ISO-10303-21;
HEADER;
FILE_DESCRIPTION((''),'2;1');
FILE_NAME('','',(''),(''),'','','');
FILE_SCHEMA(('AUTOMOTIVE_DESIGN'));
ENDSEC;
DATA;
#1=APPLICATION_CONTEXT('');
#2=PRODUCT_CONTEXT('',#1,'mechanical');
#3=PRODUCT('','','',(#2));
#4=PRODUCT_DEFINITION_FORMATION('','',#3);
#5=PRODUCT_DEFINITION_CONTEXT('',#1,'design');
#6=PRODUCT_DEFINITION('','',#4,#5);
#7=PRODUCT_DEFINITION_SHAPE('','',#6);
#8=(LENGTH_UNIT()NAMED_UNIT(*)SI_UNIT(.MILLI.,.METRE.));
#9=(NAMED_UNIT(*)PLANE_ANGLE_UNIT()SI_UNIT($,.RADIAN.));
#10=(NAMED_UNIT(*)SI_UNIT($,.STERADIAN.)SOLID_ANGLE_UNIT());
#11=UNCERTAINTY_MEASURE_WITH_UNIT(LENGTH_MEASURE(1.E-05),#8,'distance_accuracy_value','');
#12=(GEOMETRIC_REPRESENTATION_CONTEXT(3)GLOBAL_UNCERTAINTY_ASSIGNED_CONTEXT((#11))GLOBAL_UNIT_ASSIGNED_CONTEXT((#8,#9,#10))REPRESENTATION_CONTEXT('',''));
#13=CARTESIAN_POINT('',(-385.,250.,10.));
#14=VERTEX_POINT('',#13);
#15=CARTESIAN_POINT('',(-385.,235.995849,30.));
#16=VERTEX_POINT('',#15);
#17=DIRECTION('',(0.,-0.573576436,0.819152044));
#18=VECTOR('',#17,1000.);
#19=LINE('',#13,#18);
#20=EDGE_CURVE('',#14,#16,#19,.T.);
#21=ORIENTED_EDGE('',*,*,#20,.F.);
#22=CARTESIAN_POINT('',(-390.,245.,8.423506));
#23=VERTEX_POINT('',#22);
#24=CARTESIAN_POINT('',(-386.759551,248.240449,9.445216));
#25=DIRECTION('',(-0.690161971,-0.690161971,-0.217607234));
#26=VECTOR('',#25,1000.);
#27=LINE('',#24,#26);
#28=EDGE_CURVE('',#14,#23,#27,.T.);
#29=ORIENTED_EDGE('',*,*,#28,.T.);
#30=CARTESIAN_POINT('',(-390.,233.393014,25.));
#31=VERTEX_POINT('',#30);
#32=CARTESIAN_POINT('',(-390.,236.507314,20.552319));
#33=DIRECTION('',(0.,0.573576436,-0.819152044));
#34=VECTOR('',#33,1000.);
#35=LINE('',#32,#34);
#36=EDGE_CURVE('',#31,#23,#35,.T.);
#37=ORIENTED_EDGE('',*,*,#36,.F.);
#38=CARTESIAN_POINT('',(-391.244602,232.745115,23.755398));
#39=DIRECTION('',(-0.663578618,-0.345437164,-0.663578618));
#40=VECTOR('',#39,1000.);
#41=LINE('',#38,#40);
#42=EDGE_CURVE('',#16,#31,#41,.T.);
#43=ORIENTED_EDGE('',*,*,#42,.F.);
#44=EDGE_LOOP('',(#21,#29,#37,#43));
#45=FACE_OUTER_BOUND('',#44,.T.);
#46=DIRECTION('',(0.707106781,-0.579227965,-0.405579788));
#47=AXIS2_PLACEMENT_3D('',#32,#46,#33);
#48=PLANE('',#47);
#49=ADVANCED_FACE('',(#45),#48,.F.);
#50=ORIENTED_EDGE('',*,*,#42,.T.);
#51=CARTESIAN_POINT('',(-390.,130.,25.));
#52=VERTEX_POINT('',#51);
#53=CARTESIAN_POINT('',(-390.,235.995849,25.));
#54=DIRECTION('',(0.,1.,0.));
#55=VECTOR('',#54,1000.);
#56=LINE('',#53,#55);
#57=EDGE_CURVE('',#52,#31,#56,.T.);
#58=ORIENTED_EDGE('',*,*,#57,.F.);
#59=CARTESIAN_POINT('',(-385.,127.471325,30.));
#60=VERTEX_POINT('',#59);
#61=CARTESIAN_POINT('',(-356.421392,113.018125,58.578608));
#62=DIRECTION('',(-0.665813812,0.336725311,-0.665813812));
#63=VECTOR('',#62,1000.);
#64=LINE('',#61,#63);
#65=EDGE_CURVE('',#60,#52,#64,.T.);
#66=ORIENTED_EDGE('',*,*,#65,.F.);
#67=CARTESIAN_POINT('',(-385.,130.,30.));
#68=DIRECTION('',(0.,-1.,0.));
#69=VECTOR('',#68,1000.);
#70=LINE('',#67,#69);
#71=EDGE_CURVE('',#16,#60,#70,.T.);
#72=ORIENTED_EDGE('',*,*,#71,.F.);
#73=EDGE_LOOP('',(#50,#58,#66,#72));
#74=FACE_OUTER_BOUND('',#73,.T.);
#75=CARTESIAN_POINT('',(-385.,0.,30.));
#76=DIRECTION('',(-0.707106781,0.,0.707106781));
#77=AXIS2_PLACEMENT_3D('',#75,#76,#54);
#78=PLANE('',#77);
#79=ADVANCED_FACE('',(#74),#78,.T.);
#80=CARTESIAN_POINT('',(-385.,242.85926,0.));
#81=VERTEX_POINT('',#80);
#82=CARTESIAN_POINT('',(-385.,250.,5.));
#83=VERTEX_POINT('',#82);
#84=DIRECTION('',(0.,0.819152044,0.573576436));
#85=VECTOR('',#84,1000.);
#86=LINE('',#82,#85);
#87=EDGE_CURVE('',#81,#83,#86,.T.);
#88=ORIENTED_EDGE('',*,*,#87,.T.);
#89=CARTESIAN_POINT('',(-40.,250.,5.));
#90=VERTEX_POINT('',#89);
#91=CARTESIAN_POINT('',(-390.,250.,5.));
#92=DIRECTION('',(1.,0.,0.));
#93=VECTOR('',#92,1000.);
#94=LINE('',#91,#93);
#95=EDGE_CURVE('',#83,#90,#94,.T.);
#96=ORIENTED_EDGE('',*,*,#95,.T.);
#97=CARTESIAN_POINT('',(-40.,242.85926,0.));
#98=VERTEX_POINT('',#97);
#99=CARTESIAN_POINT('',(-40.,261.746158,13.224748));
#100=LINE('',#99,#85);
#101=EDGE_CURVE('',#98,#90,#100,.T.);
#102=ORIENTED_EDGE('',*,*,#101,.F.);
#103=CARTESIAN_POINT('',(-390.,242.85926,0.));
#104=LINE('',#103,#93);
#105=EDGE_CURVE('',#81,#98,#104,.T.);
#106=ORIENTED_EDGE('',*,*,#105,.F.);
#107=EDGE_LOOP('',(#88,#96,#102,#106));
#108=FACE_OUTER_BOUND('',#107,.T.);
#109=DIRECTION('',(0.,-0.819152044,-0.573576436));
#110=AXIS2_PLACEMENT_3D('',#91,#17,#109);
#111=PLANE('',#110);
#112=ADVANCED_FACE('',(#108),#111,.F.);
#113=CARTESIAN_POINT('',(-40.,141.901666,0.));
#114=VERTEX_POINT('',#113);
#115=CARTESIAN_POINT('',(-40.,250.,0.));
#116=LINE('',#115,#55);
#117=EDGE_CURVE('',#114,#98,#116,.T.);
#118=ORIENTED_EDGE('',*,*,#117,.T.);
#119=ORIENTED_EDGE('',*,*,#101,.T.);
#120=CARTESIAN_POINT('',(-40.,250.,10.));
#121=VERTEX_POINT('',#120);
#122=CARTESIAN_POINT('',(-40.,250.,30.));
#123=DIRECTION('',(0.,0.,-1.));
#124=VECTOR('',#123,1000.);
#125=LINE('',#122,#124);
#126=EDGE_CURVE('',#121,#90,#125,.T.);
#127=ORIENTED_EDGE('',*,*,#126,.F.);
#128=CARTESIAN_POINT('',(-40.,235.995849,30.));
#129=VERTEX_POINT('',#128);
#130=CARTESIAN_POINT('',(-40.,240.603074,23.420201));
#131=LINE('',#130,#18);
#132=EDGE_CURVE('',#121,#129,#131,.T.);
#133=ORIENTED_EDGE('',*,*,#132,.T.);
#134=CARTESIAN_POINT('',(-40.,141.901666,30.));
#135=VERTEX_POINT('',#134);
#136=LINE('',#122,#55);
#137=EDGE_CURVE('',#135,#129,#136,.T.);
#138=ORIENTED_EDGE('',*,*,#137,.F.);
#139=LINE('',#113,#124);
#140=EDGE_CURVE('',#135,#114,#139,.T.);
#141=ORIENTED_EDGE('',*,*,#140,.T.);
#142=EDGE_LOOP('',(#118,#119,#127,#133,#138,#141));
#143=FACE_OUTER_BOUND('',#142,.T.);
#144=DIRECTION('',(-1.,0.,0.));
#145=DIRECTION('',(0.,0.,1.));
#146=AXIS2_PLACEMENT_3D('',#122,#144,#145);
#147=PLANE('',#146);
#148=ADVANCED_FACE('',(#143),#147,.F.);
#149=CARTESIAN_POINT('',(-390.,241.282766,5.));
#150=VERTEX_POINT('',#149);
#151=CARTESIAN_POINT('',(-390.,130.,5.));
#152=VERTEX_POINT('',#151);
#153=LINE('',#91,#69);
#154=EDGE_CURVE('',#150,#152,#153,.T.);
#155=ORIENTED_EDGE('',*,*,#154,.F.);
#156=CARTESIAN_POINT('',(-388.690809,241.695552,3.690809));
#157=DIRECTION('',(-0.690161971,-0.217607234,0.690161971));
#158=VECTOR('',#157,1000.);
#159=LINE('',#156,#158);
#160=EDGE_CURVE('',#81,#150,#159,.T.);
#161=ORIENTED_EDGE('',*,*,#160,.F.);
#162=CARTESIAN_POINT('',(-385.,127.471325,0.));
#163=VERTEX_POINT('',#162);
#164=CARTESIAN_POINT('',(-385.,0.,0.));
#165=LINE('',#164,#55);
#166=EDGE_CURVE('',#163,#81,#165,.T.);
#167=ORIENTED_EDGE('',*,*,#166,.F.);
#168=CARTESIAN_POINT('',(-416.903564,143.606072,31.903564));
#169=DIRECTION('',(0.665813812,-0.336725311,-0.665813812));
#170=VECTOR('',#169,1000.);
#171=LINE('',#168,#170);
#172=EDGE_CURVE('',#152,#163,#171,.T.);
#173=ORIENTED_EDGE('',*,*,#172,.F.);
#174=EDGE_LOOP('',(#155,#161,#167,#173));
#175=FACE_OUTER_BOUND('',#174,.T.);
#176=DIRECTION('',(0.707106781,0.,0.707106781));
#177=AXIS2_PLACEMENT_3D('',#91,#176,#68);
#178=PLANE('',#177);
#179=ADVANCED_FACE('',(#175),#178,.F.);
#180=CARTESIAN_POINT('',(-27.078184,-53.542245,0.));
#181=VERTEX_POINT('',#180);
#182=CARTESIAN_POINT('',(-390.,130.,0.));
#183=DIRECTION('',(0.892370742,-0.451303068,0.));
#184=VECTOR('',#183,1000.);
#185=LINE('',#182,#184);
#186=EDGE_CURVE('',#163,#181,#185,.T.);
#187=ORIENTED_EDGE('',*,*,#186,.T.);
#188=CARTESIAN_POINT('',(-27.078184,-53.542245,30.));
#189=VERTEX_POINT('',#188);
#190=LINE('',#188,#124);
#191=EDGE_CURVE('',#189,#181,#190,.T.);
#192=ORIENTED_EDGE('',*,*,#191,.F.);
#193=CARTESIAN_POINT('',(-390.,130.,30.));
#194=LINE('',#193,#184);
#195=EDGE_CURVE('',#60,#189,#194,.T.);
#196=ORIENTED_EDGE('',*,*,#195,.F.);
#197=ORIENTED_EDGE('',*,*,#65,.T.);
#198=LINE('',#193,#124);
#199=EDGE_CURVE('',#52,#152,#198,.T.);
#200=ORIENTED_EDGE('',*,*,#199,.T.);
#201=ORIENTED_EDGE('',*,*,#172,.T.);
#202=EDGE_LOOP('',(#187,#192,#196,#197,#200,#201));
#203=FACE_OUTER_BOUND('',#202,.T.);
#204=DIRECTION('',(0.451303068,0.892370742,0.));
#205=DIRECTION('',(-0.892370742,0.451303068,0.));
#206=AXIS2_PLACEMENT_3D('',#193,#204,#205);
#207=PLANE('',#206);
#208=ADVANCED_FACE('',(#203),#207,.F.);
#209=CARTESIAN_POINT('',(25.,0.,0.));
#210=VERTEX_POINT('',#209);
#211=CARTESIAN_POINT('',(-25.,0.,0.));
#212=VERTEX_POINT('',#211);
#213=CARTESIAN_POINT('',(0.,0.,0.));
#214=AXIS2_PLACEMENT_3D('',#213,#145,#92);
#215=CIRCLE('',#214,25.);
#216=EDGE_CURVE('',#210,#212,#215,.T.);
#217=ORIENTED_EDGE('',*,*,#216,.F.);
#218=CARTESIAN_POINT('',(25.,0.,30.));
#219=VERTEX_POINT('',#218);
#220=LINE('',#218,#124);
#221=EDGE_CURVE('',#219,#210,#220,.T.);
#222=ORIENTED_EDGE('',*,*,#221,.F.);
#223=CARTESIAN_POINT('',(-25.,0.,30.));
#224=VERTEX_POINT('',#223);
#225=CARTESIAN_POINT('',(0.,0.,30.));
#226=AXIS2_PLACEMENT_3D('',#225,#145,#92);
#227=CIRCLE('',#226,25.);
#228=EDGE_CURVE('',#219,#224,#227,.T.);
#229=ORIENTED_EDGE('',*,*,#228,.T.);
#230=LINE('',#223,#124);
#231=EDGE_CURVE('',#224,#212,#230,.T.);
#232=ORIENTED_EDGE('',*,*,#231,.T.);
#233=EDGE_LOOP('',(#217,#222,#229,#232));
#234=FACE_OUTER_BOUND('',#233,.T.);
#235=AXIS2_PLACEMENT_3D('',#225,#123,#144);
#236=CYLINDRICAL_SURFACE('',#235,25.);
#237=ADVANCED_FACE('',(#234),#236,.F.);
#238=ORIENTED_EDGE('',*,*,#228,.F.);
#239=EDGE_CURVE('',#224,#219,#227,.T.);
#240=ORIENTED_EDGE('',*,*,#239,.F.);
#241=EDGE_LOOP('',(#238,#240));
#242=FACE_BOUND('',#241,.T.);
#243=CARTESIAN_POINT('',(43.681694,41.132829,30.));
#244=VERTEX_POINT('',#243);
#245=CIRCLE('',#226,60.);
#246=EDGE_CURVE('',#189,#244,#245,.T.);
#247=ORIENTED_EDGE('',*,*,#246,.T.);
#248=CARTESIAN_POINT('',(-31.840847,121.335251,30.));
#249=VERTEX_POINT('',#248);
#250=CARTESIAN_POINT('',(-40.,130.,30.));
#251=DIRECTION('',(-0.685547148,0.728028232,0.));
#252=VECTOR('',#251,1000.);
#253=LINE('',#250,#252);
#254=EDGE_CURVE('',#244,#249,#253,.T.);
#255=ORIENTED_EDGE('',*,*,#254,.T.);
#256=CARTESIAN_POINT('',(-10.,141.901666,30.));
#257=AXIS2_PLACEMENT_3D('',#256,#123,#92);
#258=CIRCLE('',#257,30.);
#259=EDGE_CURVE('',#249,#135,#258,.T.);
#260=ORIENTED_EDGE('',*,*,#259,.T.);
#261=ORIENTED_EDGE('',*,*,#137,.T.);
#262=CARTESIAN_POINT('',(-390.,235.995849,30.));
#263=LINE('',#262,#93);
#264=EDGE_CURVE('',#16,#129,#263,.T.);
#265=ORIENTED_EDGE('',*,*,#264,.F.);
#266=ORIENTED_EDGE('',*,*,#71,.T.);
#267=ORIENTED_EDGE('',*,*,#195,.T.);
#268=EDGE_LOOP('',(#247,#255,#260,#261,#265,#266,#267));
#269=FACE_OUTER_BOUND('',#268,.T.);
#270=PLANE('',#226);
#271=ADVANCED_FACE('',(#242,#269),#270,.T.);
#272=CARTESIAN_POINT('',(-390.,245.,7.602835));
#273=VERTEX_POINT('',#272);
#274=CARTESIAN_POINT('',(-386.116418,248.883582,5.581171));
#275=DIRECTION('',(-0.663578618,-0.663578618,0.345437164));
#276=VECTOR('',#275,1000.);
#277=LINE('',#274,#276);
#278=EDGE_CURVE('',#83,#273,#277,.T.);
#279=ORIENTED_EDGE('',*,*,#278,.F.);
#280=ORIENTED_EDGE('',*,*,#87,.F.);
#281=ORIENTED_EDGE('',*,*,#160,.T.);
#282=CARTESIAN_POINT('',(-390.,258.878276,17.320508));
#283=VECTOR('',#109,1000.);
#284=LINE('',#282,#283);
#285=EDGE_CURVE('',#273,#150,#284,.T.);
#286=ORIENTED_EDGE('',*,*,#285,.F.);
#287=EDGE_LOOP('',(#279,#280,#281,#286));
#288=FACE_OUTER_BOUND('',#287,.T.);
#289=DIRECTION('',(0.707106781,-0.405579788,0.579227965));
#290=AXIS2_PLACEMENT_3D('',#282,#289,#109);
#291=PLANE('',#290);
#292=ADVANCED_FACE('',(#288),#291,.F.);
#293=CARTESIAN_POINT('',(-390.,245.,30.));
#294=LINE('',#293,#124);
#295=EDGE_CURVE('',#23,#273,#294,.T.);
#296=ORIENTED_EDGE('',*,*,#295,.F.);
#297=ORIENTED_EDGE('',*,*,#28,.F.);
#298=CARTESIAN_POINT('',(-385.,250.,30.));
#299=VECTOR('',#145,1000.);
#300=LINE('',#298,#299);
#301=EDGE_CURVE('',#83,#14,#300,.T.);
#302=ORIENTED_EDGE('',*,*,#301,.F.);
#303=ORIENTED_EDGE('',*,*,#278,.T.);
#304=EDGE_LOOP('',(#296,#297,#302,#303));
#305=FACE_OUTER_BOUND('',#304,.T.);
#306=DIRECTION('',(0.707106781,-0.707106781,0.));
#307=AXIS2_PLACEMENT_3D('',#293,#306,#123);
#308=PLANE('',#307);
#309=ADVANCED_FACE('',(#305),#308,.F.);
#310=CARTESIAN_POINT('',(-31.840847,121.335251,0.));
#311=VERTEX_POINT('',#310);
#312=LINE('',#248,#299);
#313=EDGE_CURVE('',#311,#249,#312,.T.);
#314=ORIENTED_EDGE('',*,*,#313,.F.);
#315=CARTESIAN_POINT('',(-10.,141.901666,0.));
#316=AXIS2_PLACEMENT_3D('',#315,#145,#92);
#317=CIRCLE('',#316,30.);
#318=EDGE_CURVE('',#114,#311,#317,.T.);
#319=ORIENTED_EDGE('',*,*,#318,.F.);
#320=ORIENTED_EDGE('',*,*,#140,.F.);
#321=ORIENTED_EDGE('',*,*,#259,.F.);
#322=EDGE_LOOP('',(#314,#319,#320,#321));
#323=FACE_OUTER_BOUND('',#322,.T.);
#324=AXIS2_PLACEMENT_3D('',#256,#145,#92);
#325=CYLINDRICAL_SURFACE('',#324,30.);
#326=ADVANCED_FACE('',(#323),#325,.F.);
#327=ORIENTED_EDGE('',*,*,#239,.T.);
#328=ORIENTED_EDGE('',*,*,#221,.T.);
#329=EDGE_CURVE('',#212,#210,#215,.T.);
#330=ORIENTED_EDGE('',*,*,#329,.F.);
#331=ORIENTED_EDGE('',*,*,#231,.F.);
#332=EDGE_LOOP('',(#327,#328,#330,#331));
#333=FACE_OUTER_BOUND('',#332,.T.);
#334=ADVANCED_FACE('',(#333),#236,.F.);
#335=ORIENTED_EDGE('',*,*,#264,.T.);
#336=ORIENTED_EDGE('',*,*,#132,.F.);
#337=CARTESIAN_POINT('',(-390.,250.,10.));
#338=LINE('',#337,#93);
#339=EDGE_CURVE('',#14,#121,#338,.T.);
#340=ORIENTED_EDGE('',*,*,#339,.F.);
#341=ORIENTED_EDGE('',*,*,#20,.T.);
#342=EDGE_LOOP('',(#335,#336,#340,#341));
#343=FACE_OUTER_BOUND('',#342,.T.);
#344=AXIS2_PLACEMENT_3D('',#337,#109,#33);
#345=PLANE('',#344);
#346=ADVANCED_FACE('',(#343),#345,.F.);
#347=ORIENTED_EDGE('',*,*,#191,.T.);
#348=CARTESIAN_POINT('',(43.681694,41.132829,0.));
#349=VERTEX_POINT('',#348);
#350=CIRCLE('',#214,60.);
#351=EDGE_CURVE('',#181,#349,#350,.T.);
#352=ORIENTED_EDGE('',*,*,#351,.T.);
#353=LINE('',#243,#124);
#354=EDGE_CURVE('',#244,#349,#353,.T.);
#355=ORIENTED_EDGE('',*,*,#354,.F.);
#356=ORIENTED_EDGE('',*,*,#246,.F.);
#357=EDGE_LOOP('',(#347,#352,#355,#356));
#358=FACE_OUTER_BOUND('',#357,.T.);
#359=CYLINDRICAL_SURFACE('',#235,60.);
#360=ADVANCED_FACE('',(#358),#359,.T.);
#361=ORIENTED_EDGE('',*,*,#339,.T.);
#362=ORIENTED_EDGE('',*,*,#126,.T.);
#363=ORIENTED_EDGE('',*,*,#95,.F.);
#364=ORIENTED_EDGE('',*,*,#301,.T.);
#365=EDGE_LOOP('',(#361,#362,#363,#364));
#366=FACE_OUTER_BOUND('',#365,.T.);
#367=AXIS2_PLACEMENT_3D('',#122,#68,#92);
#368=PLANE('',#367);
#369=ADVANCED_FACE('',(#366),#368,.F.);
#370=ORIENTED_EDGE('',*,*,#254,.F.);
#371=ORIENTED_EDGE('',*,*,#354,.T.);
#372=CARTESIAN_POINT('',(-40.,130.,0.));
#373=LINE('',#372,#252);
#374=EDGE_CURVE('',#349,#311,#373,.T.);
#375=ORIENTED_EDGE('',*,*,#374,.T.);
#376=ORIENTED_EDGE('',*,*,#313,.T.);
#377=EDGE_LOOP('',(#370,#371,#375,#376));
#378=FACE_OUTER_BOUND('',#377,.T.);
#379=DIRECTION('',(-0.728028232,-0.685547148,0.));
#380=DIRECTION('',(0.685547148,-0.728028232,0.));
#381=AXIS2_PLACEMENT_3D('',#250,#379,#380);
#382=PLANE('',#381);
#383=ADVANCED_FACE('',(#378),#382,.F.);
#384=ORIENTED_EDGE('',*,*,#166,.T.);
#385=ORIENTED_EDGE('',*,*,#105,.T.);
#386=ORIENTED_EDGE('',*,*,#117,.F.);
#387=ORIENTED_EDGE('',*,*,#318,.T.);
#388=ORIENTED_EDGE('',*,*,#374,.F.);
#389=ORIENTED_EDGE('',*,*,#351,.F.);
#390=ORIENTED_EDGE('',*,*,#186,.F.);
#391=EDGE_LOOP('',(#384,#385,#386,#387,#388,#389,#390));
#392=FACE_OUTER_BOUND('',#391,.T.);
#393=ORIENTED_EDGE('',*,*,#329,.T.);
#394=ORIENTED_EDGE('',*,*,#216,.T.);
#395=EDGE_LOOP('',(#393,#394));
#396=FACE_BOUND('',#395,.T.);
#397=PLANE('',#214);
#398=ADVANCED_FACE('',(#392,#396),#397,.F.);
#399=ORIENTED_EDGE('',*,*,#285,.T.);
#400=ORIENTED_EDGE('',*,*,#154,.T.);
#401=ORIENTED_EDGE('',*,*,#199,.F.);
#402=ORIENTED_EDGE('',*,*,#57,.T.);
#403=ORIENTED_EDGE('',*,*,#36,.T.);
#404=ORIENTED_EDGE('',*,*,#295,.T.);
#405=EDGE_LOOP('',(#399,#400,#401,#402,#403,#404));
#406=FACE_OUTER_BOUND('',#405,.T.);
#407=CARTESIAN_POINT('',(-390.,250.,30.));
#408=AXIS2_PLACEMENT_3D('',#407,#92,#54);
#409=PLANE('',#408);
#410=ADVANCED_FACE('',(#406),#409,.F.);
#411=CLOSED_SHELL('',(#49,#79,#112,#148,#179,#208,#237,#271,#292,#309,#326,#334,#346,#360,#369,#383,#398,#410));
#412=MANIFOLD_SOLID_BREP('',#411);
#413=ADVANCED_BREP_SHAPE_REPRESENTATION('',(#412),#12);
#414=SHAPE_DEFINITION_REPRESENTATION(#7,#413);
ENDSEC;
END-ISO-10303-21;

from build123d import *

# Parameters (mm, degrees)
SKETCH_1_R          = 25
EXTRUDE_1_DEPTH     = 30
CUT_EXTRUDE_2_DEPTH = 516.654923374
CUT_EXTRUDE_3_DEPTH = 516.654923374
CHAMFER_1_SIZE      = 5
FILLET_2_R          = 30


with BuildPart() as part:
    # 草图1 → 凸台-拉伸1 (new body)
    with BuildSketch(Plane.XY):
        with BuildLine():
            Line((-40, 250), (-390, 250))
            Line((-390, 250), (-390, 130))
            Line((-390, 130), (-27.078184069, -53.542244514))
            ThreePointArc((-27.078184069, -53.542244514), (48.059978328, -35.919889798), (43.681693947, 41.132828907))
            Line((43.681693947, 41.132828907), (-40, 130))
            Line((-40, 130), (-40, 250))
        make_face()
        Circle(SKETCH_1_R, mode=Mode.SUBTRACT)
    extrude(amount=EXTRUDE_1_DEPTH)

    # 草图2 → 切除-拉伸2 (cut, through all)
    with BuildSketch(Plane(origin=(60, 0, 0), x_dir=(0, 0, -1), z_dir=(1, 0, 0))):
        Polygon((-10, 250), (-30, 235.995849236), (-30, 250), align=None)
    extrude(amount=-CUT_EXTRUDE_2_DEPTH, mode=Mode.SUBTRACT)

    # 草图3 → 切除-拉伸3 (cut, through all)
    with BuildSketch(Plane(origin=(60, 0, 0), x_dir=(0, 0, -1), z_dir=(1, 0, 0))):
        Polygon((-5, 250), (0, 242.859259966), (0, 250), align=None)
    extrude(amount=-CUT_EXTRUDE_3_DEPTH, mode=Mode.SUBTRACT)

    # 倒角1
    chamfer_1_edges = [part.edges().sort_by_distance(p)[0] for p in [
        (-390, 182.997924618, 30),
        (-390, 250, 7.5),
        (-390, 242.997924618, 20),
        (-390, 186.429629983, 0),
        (-390, 246.429629983, 2.5),
    ]]
    chamfer(chamfer_1_edges, length=CHAMFER_1_SIZE)

    # 圆角2
    fillet_2_edges = [part.edges().sort_by_distance(p)[0] for p in [
        (-40, 130, 15),
    ]]
    fillet(fillet_2_edges, radius=FILLET_2_R)


solid = part.part
